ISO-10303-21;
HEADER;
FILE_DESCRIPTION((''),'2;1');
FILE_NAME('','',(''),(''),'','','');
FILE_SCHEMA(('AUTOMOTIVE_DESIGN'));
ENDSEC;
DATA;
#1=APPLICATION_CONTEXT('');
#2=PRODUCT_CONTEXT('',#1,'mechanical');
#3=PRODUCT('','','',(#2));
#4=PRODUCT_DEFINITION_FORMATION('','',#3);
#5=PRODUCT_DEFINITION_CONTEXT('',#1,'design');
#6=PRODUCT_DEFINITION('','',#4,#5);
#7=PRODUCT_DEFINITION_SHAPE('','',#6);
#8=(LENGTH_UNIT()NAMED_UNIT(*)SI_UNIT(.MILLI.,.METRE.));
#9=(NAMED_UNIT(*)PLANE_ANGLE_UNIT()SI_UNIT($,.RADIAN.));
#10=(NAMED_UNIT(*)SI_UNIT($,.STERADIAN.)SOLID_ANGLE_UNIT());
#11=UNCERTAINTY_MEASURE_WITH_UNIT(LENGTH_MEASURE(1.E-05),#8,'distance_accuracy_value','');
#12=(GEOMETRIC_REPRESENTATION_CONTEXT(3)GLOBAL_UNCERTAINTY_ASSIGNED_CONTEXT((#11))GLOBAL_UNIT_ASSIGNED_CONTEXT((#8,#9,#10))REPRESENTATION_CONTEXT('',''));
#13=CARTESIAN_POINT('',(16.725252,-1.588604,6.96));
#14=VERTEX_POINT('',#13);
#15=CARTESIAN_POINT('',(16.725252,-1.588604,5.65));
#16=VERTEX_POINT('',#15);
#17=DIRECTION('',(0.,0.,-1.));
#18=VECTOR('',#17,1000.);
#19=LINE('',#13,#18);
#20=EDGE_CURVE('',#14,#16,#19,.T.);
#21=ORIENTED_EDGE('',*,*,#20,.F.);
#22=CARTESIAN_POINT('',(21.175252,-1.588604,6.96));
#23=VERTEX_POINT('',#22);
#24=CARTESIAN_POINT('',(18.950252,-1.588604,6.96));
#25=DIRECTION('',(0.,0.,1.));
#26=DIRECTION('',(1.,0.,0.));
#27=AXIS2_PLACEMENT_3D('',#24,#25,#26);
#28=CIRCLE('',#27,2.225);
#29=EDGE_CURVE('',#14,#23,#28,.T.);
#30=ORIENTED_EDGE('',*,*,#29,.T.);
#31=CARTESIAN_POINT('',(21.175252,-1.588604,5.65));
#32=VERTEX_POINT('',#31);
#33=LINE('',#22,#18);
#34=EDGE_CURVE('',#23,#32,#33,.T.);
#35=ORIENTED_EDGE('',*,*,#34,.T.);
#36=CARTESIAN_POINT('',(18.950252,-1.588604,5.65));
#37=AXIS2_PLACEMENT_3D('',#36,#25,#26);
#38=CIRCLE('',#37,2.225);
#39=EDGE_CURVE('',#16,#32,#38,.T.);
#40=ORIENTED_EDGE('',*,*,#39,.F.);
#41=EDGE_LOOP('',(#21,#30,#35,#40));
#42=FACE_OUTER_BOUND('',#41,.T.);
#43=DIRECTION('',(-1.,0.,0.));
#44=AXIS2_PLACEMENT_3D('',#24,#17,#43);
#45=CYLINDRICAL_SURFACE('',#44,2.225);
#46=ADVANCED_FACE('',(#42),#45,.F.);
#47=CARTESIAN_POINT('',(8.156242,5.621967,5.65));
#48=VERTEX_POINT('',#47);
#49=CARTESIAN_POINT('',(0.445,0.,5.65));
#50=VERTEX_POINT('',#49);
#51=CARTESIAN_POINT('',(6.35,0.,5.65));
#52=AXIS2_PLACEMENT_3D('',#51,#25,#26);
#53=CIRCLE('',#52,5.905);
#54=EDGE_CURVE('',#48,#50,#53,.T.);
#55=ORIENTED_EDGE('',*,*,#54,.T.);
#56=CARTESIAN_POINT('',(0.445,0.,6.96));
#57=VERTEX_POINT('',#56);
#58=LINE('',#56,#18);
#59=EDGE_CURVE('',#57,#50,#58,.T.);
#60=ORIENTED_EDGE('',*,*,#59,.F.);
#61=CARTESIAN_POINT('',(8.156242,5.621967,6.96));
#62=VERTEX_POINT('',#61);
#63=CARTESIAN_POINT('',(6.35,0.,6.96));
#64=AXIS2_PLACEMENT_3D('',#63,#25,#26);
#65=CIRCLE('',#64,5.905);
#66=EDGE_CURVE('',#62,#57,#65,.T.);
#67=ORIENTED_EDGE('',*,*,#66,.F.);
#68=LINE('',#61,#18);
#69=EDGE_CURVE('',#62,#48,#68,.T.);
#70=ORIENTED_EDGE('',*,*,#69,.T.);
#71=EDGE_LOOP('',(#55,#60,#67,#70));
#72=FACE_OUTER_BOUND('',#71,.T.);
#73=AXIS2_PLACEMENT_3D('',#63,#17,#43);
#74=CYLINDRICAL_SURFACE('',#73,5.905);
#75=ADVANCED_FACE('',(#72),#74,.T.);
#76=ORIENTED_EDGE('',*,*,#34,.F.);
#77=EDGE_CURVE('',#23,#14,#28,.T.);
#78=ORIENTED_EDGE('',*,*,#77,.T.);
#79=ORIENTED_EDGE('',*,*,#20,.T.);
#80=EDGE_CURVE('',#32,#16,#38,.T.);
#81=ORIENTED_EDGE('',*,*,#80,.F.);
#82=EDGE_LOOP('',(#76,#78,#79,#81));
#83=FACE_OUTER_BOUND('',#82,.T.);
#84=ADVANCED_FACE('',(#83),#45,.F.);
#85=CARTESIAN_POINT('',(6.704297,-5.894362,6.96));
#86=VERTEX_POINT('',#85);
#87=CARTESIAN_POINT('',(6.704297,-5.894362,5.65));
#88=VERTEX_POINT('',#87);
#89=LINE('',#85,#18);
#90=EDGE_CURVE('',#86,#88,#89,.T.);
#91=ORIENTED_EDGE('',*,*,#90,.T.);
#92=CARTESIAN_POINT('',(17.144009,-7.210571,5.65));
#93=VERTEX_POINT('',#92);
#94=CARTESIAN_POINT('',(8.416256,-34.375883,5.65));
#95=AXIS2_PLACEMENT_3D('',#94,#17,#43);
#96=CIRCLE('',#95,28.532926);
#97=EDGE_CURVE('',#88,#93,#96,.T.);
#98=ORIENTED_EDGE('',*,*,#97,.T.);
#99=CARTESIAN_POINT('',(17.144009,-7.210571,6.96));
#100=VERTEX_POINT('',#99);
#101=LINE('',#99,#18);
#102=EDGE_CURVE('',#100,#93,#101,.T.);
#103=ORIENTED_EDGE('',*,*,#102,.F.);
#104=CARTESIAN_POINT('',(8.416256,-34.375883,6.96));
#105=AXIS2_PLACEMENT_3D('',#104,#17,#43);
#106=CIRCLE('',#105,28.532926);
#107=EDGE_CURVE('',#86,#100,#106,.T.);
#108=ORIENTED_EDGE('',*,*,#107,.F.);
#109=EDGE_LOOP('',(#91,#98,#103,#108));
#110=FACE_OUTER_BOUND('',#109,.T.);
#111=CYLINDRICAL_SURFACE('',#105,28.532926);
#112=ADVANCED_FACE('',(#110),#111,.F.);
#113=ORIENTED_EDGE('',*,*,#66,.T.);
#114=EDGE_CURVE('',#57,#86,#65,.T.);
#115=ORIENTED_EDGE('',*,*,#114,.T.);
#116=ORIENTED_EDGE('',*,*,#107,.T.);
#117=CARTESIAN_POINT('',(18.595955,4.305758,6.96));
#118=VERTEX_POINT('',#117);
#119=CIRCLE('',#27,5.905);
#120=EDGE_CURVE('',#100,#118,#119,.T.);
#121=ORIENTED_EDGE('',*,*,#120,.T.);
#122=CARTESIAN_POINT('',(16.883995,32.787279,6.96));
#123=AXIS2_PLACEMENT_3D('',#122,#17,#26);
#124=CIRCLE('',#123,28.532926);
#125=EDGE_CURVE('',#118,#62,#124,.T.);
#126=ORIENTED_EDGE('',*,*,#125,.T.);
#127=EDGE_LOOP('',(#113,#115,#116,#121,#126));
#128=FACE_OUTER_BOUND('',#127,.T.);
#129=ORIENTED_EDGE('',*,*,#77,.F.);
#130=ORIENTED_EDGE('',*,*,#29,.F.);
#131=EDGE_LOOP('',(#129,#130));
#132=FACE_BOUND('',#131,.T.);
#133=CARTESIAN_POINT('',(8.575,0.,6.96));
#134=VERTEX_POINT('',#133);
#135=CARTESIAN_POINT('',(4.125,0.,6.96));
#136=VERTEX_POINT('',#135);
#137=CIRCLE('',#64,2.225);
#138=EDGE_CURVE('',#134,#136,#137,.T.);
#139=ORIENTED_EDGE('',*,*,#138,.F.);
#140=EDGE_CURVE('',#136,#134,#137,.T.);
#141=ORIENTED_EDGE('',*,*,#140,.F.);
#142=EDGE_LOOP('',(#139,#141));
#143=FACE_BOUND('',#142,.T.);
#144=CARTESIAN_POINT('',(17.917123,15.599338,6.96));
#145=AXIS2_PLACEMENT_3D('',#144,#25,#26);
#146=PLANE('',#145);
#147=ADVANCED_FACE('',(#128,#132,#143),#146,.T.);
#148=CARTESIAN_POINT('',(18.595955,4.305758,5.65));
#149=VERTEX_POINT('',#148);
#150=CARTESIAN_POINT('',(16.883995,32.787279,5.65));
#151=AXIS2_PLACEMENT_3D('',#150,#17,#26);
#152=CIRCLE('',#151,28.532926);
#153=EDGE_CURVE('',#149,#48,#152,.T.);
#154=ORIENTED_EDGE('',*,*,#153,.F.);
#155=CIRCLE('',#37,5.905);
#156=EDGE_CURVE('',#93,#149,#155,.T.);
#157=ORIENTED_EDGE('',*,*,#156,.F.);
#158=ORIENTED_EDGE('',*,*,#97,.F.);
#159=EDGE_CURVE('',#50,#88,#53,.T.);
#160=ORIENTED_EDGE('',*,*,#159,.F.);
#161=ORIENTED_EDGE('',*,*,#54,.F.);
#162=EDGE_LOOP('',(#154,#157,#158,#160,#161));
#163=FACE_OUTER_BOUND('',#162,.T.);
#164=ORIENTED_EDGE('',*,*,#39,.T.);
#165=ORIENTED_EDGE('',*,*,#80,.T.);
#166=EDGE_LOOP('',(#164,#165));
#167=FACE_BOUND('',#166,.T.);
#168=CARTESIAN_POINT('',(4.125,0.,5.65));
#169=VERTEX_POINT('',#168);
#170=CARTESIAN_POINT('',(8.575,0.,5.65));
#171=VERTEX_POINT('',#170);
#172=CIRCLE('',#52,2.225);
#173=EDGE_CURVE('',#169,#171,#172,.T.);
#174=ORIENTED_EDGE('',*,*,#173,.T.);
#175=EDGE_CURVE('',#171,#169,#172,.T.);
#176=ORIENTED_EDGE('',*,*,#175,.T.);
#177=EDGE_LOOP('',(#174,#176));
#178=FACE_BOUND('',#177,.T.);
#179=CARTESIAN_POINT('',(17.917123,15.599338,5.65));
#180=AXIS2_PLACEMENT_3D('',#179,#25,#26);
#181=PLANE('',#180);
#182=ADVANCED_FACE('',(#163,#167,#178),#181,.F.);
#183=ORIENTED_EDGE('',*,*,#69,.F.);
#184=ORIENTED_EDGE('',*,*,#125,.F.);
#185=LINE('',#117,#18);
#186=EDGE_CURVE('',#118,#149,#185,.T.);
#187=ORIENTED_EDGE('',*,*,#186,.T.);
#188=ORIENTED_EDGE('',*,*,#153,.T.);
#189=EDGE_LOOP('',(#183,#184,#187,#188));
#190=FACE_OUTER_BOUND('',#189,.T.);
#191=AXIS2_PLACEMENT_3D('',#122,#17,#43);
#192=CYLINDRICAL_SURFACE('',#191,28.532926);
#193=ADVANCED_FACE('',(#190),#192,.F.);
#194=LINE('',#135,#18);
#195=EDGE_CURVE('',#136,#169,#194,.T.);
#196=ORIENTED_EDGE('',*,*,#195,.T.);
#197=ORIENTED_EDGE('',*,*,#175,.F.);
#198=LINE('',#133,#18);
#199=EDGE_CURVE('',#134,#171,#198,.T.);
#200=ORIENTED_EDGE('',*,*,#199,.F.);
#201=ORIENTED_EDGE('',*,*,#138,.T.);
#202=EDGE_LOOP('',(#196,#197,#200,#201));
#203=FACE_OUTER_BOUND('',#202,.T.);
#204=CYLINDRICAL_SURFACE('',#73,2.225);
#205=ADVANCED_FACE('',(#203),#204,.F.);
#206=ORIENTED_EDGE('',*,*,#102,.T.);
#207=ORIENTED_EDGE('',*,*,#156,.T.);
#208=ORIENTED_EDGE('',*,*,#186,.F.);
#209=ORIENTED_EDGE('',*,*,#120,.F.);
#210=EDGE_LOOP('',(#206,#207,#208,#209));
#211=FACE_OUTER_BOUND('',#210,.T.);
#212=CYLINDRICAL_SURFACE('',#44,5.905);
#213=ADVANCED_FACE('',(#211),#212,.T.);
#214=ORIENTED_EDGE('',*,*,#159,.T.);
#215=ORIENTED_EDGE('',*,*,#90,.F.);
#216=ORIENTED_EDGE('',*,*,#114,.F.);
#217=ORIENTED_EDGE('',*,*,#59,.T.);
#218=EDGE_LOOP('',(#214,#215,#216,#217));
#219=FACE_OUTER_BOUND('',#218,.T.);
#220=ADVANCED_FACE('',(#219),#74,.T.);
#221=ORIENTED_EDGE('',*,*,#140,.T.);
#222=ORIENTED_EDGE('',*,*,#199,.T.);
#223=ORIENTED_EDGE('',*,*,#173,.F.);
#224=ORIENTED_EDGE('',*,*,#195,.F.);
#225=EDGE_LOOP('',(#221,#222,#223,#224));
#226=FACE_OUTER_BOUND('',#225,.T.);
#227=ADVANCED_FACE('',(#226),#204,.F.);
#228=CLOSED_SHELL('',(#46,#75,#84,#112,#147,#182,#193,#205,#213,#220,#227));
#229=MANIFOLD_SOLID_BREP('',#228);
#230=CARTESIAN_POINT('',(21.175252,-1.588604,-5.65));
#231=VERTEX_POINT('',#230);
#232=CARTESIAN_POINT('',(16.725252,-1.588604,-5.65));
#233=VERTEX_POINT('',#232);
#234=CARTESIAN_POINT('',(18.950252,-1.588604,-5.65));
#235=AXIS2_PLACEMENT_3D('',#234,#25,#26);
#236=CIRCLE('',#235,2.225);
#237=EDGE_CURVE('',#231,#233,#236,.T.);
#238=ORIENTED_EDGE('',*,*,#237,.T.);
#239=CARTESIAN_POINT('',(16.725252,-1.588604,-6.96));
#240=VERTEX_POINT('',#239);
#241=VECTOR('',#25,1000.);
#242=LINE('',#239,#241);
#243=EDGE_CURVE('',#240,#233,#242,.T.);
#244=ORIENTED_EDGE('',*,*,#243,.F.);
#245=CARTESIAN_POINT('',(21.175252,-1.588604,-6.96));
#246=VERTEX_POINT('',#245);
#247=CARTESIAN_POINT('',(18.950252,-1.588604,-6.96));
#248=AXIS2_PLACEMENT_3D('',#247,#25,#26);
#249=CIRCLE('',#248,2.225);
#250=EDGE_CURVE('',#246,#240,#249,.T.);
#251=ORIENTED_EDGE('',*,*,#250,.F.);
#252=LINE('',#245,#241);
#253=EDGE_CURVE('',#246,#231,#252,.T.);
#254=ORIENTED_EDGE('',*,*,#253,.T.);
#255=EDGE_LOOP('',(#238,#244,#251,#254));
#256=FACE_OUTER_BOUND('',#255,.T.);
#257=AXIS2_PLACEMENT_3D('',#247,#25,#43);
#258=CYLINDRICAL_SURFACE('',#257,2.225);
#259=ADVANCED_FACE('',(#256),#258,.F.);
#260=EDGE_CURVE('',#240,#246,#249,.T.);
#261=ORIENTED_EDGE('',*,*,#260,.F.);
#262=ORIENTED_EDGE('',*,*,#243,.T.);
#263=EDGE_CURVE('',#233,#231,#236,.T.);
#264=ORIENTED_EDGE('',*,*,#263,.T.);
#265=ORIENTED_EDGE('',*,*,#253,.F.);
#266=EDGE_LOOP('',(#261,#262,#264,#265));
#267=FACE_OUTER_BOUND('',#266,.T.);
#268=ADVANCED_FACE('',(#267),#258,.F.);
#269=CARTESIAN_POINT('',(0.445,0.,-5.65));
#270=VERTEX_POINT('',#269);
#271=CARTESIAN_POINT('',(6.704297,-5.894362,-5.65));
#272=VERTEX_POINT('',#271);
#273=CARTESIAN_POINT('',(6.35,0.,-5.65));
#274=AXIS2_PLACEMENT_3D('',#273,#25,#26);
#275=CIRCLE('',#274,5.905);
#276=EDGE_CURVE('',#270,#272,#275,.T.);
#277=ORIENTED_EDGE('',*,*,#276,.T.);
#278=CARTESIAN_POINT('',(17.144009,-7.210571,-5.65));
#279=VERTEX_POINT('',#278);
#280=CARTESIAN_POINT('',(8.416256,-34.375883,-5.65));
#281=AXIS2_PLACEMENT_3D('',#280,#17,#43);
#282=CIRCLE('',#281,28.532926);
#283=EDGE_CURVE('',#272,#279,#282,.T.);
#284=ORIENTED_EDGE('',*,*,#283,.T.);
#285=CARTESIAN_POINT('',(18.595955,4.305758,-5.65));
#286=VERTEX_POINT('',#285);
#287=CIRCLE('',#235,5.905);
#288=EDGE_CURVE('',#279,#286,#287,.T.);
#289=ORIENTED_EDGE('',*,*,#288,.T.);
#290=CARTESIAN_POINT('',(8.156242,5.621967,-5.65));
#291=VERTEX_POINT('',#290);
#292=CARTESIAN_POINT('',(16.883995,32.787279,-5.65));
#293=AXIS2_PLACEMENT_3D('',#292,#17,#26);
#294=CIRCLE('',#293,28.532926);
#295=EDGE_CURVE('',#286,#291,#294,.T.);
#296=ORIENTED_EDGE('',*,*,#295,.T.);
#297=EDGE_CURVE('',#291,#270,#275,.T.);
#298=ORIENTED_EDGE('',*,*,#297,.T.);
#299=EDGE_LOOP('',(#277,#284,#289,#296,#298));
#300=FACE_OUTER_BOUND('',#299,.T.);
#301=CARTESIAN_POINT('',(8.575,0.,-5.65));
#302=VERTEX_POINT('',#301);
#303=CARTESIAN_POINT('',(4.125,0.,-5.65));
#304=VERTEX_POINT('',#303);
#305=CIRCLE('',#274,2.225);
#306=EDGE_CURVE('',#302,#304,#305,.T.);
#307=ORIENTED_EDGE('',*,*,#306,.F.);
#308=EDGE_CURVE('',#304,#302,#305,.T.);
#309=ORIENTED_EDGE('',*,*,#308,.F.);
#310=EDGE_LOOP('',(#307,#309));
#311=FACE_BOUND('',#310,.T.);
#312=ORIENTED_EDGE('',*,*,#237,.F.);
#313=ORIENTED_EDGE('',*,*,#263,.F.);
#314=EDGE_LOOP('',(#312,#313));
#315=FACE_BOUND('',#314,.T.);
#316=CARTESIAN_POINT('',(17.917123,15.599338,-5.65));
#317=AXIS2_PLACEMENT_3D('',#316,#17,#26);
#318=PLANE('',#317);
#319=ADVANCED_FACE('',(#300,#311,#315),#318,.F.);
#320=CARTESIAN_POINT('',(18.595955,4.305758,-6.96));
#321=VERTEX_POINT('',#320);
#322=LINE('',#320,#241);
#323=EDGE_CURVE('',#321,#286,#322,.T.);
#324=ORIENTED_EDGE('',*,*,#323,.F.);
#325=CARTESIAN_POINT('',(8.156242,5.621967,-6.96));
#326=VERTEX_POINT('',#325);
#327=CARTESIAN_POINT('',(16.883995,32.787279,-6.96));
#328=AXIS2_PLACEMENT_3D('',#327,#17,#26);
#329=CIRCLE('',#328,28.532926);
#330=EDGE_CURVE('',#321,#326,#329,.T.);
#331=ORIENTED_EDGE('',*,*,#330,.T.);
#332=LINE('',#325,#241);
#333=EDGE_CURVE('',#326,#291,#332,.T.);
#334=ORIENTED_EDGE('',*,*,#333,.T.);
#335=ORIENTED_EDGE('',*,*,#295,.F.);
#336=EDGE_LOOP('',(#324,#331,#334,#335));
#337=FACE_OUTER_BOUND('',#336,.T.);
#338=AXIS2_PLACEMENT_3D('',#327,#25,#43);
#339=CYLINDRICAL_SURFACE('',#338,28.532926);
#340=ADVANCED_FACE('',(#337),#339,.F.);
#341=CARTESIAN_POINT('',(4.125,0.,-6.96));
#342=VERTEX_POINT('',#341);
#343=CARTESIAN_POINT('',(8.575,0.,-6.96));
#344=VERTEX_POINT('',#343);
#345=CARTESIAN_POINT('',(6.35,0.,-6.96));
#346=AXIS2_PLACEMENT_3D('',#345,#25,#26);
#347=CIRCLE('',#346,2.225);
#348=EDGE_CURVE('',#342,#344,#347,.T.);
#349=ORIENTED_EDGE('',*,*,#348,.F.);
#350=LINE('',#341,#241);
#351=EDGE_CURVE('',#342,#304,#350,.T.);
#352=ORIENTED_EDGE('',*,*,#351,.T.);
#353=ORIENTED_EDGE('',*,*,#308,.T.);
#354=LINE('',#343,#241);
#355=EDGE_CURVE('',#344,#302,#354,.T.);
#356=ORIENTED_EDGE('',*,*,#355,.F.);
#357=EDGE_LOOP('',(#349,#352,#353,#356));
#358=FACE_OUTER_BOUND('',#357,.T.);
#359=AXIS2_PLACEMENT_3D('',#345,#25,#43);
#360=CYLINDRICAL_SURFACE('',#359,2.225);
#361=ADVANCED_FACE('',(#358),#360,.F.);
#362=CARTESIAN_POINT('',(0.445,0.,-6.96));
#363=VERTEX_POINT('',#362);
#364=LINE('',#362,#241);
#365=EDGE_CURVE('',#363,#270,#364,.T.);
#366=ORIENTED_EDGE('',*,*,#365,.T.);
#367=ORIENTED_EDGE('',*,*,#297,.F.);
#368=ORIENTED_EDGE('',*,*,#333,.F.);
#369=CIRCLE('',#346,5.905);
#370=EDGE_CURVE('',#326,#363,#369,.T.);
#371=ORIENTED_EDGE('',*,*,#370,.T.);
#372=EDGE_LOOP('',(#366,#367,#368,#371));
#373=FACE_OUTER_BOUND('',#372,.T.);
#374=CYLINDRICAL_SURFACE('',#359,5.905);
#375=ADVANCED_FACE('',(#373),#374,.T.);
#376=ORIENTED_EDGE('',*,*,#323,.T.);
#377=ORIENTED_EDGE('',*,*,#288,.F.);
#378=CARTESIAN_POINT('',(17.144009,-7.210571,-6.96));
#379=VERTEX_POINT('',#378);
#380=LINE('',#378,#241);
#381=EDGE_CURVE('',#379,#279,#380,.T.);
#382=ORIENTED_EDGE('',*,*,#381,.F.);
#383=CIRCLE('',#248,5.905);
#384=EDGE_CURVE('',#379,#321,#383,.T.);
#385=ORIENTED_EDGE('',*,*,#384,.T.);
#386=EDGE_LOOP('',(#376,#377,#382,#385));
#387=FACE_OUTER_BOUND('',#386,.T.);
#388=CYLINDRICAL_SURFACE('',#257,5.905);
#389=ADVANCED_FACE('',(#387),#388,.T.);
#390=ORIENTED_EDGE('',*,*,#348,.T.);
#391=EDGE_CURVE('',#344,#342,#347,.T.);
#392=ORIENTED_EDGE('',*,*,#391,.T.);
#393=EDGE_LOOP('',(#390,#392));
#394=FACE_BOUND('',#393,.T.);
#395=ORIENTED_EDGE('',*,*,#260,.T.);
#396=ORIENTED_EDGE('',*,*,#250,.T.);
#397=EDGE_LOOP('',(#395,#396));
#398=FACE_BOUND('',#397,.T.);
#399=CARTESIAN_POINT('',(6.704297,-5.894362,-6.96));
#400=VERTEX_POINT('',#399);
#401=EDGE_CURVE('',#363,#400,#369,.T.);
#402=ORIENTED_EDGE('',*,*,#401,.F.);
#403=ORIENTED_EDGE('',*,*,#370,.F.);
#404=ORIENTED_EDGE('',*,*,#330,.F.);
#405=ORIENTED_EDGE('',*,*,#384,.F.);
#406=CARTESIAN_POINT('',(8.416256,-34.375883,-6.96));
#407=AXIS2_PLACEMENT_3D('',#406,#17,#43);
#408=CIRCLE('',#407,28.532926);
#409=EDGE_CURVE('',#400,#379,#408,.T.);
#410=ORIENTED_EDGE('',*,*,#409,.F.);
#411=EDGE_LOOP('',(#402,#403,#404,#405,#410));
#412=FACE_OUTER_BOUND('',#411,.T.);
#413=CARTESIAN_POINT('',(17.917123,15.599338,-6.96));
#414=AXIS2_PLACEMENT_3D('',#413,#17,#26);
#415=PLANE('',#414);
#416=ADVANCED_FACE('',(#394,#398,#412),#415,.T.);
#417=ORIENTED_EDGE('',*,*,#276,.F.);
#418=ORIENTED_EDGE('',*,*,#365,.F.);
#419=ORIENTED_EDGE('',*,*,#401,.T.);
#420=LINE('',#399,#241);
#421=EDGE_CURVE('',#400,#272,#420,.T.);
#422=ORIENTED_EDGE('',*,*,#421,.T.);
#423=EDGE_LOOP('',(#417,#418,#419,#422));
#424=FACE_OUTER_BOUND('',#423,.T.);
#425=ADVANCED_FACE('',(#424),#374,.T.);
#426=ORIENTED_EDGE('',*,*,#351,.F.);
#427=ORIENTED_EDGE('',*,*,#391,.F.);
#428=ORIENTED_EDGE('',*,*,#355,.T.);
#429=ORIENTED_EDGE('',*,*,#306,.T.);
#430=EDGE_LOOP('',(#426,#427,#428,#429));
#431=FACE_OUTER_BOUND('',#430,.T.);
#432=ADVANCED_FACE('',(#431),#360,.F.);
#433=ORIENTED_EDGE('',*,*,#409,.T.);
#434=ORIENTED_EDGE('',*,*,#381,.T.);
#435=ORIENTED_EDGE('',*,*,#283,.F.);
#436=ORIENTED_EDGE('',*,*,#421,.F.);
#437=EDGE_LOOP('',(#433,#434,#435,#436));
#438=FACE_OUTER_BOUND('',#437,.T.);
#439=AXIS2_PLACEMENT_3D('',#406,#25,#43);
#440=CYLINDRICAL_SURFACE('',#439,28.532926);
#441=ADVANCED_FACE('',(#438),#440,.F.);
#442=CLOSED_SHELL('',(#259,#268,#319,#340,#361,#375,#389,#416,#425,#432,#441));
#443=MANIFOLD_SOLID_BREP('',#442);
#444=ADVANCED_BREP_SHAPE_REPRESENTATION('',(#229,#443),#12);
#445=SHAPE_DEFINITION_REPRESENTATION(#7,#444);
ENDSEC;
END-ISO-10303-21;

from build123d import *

# Parameters (mm, degrees)
SKETCH_2_R        = 4.255
EXTRUDE_1_DEPTH   = 3.875
EXTRUDE_1_2_DEPTH = 3.875
EXTRUDE_2_DEPTH   = 1.775
SKETCH_6_R        = 2.225
EXTRUDE_4_DEPTH   = 1.31


with BuildPart() as part:
    # 草图2 → 拉伸1 (new, symmetric)
    with BuildSketch(Plane.XY):
        with Locations((6.35, 0)):
            Circle(SKETCH_2_R)
    extrude(amount=EXTRUDE_1_DEPTH, both=True)



with BuildPart() as body_2:
    # 草图2 → Extrude 1 2 (new, symmetric)
    with BuildSketch(Plane.XY):
        with Locations((-6.35, 0)):
            Circle(SKETCH_2_R)
    extrude(amount=EXTRUDE_1_2_DEPTH, both=True)


with BuildPart() as part_1:
    add(part.part)

    add(body_2.part)  # 拉伸2 merges body 2
    # 草图3 → 拉伸2 (add)
    with BuildSketch(Plane.XY.offset(3.875)):
        with BuildLine():
            ThreePointArc((-5.261178614, 5.803748184), (-12.255, 0), (-5.261178614, -5.803748184))
            ThreePointArc((-5.261178614, -5.803748184), (0, -5.3145), (5.261178614, -5.803748184))
            ThreePointArc((5.261178614, -5.803748184), (12.255, 0), (5.261178614, 5.803748184))
            ThreePointArc((5.261178614, 5.803748184), (0, 5.3145), (-5.261178614, 5.803748184))
        make_face()
    extrude(amount=EXTRUDE_2_DEPTH)


with BuildPart() as body_2_2:
    # 草图6 → 拉伸4 (new body)
    with BuildSketch(Plane.XY.offset(5.65)):
        with BuildLine():
            ThreePointArc((17.144009153, -7.210570587), (24.808872428, -2.327241646), (18.595954811, 4.305758071))
            ThreePointArc((18.595954811, 4.305758071), (13.314900062, 4.478457031), (8.156242384, 5.621967045))
            ThreePointArc((8.156242384, 5.621967045), (0.491379108, 0.738638104), (6.704296726, -5.894361613))
            ThreePointArc((6.704296726, -5.894361613), (11.985351475, -6.067060574), (17.144009153, -7.210570587))
        make_face()
        with Locations(Location((6.35, 0, 0), (0, 0, 180))):
            Circle(SKETCH_6_R, mode=Mode.SUBTRACT)
        with Locations(Location((18.950251537, -1.588603542, 0), (0, 0, 180))):
            Circle(SKETCH_6_R, mode=Mode.SUBTRACT)
    extrude(amount=EXTRUDE_4_DEPTH)


with BuildPart() as body_2_3:
    # 镜向1: mirrored copy
    add(body_2_2.part.mirror(Plane(origin=(0, 0, 0), x_dir=(1, 0, 0), z_dir=(0, 0, -1))))


solid = Compound([body_2_2.part, body_2_3.part])
